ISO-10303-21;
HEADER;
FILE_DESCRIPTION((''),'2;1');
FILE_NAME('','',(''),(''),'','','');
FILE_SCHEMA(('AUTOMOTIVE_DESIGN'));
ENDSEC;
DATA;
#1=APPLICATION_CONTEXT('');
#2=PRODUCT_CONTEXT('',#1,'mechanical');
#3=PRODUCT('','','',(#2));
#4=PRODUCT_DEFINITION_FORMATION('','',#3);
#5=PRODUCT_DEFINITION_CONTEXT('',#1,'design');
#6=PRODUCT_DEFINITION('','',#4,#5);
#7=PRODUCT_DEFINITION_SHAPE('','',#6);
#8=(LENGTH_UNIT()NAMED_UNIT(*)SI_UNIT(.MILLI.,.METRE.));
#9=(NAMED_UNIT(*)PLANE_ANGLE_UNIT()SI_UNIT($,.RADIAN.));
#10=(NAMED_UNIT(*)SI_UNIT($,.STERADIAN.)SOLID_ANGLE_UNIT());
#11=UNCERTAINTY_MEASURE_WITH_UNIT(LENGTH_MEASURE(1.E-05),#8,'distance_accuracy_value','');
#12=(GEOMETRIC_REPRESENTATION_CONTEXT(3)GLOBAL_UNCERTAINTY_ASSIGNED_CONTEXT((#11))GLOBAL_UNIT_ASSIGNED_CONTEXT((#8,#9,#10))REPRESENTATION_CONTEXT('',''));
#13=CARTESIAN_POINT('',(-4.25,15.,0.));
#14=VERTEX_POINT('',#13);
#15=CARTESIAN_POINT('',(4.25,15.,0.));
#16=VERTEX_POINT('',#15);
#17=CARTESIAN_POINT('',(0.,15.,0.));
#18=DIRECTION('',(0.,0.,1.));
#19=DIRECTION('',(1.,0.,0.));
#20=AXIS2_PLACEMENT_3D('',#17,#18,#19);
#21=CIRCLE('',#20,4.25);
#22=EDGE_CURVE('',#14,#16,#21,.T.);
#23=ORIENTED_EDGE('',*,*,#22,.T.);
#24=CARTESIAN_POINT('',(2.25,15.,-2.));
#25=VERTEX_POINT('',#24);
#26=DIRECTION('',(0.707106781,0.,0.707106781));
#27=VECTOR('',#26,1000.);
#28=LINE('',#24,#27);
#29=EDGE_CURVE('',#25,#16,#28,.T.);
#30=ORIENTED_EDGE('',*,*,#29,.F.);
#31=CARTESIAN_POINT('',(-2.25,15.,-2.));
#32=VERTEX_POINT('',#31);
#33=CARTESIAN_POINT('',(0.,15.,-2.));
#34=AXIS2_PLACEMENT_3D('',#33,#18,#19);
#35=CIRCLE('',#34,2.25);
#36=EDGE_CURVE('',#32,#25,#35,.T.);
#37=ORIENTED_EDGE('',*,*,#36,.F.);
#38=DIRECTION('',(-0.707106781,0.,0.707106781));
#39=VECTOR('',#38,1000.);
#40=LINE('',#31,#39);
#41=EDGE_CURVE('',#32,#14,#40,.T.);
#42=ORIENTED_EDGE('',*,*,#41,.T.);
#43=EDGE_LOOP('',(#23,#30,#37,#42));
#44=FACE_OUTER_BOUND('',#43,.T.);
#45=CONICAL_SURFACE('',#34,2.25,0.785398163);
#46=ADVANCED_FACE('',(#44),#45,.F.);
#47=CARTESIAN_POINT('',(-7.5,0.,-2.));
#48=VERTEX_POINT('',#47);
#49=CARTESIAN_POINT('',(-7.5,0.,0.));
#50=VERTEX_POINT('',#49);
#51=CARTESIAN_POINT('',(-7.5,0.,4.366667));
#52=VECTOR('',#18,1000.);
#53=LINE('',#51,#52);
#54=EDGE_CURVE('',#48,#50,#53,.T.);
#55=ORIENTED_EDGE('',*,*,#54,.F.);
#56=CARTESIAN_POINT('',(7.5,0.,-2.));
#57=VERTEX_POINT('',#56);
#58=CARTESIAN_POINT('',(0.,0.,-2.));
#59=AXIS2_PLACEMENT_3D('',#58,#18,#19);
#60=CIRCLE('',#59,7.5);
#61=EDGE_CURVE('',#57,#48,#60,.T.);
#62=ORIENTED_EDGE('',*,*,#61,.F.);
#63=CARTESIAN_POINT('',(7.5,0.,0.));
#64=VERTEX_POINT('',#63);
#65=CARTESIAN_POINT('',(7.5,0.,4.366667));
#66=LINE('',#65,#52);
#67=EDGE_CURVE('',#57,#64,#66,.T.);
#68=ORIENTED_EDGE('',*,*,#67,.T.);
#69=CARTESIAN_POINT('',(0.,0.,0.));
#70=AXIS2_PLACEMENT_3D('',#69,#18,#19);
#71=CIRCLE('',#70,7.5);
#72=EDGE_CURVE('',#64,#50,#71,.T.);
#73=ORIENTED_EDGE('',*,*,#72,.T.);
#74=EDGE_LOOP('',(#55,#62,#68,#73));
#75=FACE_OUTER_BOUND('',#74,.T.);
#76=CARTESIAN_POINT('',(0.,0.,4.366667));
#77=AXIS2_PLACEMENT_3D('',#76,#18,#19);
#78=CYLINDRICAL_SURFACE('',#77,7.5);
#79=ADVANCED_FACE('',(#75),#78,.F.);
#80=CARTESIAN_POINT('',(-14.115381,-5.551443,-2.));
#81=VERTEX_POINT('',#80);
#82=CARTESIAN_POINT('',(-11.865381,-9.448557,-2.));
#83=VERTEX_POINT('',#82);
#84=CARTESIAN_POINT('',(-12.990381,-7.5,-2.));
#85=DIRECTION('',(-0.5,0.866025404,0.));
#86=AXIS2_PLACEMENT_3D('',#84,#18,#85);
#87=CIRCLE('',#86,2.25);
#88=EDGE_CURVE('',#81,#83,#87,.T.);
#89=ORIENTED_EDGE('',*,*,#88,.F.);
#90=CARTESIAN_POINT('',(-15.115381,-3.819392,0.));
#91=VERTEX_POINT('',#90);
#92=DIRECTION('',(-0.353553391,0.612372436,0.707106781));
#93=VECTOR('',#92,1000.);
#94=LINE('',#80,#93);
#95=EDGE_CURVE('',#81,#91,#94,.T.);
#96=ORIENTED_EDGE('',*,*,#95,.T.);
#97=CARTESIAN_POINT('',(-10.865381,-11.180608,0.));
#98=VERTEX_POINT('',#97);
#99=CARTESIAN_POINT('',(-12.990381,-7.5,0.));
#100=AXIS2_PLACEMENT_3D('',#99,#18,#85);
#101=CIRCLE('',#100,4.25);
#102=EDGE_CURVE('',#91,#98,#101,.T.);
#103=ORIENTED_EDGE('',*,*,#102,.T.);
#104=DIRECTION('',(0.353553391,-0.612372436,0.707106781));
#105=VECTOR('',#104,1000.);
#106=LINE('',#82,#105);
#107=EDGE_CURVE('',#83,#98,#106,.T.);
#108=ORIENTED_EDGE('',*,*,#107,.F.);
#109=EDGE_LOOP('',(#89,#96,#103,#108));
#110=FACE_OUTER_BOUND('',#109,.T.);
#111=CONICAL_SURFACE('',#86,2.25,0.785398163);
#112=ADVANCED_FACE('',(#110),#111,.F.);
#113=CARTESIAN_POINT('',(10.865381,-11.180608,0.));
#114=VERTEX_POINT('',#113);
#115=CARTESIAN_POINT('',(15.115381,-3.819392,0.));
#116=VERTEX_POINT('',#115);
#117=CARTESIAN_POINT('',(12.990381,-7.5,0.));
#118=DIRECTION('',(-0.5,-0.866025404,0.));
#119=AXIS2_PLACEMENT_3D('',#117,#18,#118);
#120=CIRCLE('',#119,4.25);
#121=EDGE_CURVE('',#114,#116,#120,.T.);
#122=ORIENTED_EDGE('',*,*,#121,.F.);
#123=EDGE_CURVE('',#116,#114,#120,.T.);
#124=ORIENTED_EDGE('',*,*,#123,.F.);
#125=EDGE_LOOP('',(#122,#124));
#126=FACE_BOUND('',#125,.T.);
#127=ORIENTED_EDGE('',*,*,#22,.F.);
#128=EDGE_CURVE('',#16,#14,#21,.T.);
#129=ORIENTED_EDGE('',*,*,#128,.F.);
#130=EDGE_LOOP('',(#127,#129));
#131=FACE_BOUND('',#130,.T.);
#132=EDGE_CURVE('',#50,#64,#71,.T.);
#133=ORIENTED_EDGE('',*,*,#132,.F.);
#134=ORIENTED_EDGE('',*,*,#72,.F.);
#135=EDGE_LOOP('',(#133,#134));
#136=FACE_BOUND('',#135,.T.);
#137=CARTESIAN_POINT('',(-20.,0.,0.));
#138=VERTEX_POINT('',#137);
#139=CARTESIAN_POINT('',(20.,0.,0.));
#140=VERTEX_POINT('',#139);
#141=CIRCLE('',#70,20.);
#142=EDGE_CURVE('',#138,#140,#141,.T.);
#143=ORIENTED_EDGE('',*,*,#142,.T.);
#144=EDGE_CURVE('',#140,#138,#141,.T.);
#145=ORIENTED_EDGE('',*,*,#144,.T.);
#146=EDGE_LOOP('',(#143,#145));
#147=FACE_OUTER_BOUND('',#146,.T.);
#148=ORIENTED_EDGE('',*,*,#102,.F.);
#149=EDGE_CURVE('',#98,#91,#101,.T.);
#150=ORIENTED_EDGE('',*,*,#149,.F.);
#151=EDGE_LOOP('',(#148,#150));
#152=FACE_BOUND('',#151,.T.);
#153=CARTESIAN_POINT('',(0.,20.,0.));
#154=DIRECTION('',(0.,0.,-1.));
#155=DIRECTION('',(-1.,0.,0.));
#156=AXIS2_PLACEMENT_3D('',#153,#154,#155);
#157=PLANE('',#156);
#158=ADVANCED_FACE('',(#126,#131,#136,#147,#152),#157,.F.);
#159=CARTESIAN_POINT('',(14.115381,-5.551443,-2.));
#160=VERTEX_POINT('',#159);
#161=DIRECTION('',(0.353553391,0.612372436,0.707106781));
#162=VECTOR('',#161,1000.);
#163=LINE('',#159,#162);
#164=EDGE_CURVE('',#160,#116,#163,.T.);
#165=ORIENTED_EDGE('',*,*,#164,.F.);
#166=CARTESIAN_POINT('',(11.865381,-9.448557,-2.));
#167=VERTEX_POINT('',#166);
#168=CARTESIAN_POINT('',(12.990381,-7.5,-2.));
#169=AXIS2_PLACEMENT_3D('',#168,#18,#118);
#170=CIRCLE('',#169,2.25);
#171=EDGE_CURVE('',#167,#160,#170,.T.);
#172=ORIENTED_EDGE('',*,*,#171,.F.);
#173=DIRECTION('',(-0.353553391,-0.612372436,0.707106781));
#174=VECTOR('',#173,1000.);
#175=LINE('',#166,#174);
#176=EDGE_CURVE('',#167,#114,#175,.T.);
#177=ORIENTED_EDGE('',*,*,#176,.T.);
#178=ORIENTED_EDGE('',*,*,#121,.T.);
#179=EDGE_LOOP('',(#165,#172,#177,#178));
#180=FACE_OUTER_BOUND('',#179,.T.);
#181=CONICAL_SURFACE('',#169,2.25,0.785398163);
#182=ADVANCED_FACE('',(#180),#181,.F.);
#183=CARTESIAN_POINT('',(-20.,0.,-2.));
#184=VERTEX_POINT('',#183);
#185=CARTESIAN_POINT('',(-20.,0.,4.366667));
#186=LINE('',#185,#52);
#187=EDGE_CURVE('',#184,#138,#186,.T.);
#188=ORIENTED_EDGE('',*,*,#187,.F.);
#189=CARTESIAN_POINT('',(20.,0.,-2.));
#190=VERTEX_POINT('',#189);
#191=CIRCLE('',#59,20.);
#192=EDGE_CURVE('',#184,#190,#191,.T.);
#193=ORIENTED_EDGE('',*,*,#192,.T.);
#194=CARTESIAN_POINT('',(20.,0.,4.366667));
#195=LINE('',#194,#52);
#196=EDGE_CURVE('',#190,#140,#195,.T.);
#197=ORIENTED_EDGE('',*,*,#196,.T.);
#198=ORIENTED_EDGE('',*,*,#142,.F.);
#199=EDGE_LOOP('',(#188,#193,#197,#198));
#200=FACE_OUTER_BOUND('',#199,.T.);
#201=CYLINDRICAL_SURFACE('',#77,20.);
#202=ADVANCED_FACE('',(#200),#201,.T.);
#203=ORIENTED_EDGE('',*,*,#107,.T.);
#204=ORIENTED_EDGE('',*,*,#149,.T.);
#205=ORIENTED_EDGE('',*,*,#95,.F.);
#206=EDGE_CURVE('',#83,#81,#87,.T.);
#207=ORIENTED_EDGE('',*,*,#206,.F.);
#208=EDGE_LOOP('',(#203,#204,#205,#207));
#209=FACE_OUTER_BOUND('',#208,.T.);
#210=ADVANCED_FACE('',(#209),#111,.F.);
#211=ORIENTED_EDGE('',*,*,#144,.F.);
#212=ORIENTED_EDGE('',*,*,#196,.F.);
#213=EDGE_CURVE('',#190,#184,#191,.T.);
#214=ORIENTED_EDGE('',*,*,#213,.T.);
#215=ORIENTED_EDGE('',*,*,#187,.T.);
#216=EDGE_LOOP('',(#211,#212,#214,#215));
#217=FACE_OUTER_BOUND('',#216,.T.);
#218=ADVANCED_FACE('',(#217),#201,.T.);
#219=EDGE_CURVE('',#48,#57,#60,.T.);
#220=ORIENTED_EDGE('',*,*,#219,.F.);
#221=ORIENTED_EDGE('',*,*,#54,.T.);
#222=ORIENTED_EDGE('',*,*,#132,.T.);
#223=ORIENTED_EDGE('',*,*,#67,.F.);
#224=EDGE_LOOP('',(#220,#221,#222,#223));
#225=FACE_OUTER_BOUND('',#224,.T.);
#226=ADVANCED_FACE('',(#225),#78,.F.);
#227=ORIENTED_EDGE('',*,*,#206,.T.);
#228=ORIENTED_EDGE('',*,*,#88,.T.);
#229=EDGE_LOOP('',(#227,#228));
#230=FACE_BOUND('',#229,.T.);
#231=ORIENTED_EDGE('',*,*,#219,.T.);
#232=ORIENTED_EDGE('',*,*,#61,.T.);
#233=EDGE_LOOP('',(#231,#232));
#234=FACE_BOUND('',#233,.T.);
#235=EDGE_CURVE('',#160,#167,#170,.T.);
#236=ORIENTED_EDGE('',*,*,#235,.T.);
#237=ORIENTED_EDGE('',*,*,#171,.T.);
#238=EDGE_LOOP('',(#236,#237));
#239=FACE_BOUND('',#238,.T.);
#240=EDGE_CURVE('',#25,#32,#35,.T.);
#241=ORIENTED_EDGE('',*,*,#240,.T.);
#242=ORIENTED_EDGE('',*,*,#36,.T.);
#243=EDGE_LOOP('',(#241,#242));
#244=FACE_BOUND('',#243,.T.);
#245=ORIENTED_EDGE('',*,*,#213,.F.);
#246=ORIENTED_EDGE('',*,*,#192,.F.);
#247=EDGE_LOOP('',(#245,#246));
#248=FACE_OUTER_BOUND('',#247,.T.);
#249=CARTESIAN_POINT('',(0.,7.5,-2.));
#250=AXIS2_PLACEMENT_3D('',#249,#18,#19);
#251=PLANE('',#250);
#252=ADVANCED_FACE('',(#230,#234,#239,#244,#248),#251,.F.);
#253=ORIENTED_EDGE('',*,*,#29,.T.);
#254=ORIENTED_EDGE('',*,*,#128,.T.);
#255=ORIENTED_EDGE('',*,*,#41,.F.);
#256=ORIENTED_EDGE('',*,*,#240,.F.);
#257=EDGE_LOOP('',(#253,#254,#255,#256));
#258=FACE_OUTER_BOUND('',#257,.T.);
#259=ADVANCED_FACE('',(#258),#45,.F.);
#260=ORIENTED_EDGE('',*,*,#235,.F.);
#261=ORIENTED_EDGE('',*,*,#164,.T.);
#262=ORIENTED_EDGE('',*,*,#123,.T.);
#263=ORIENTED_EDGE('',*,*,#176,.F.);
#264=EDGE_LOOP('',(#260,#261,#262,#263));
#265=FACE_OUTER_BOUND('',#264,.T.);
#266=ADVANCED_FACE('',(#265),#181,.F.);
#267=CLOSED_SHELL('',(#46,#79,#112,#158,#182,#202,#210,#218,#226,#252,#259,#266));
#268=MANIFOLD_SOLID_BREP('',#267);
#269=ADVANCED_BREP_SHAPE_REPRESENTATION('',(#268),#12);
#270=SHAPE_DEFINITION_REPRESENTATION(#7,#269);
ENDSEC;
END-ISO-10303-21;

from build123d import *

# Parameters (mm, degrees)
SKETCH1_W         = 2
SKETCH1_H         = 12.5
CIRPATTERN1_COUNT = 3


with BuildPart() as part:
    # Sketch1 → Revolve1 (revolve)
    with BuildSketch(Plane(origin=(0, 0, 0), x_dir=(0, 0, -1), z_dir=(1, 0, 0)), mode=Mode.PRIVATE) as revolve1_sk:
        with Locations((1, 13.75)):
            Rectangle(SKETCH1_W, SKETCH1_H)
    revolve(revolve1_sk.sketch.rotate(Axis((0, 0, 4.366666667), (0, 0, -1)), 90), axis=Axis((0, 0, 4.366666667), (0, 0, -1)))

    # Sketch2 → Cut-Revolve1 (revolve, cut)
    with BuildSketch(Plane(origin=(0, 0, 0), x_dir=(0, 0, -1), z_dir=(1, 0, 0)), mode=Mode.PRIVATE) as cut_revolve1_sk:
        Polygon((0, 19.25), (2, 17.25), (2, 15), (0, 15), align=None)
    cut_revolve1 = revolve(cut_revolve1_sk.sketch.rotate(Axis((0, 15, 0.909195932), (0, 0, -1)), 90), axis=Axis((0, 15, 0.909195932), (0, 0, -1)), mode=Mode.SUBTRACT)

    # CirPattern1: Cut-Revolve1 ×3 about axis
    cirpattern1_axis = Axis((0, 0, 0), (0, 0, 1))
    for i in range(1, CIRPATTERN1_COUNT):
        add(cut_revolve1.rotate(cirpattern1_axis, i * 360 / CIRPATTERN1_COUNT), mode=Mode.SUBTRACT)


solid = part.part
